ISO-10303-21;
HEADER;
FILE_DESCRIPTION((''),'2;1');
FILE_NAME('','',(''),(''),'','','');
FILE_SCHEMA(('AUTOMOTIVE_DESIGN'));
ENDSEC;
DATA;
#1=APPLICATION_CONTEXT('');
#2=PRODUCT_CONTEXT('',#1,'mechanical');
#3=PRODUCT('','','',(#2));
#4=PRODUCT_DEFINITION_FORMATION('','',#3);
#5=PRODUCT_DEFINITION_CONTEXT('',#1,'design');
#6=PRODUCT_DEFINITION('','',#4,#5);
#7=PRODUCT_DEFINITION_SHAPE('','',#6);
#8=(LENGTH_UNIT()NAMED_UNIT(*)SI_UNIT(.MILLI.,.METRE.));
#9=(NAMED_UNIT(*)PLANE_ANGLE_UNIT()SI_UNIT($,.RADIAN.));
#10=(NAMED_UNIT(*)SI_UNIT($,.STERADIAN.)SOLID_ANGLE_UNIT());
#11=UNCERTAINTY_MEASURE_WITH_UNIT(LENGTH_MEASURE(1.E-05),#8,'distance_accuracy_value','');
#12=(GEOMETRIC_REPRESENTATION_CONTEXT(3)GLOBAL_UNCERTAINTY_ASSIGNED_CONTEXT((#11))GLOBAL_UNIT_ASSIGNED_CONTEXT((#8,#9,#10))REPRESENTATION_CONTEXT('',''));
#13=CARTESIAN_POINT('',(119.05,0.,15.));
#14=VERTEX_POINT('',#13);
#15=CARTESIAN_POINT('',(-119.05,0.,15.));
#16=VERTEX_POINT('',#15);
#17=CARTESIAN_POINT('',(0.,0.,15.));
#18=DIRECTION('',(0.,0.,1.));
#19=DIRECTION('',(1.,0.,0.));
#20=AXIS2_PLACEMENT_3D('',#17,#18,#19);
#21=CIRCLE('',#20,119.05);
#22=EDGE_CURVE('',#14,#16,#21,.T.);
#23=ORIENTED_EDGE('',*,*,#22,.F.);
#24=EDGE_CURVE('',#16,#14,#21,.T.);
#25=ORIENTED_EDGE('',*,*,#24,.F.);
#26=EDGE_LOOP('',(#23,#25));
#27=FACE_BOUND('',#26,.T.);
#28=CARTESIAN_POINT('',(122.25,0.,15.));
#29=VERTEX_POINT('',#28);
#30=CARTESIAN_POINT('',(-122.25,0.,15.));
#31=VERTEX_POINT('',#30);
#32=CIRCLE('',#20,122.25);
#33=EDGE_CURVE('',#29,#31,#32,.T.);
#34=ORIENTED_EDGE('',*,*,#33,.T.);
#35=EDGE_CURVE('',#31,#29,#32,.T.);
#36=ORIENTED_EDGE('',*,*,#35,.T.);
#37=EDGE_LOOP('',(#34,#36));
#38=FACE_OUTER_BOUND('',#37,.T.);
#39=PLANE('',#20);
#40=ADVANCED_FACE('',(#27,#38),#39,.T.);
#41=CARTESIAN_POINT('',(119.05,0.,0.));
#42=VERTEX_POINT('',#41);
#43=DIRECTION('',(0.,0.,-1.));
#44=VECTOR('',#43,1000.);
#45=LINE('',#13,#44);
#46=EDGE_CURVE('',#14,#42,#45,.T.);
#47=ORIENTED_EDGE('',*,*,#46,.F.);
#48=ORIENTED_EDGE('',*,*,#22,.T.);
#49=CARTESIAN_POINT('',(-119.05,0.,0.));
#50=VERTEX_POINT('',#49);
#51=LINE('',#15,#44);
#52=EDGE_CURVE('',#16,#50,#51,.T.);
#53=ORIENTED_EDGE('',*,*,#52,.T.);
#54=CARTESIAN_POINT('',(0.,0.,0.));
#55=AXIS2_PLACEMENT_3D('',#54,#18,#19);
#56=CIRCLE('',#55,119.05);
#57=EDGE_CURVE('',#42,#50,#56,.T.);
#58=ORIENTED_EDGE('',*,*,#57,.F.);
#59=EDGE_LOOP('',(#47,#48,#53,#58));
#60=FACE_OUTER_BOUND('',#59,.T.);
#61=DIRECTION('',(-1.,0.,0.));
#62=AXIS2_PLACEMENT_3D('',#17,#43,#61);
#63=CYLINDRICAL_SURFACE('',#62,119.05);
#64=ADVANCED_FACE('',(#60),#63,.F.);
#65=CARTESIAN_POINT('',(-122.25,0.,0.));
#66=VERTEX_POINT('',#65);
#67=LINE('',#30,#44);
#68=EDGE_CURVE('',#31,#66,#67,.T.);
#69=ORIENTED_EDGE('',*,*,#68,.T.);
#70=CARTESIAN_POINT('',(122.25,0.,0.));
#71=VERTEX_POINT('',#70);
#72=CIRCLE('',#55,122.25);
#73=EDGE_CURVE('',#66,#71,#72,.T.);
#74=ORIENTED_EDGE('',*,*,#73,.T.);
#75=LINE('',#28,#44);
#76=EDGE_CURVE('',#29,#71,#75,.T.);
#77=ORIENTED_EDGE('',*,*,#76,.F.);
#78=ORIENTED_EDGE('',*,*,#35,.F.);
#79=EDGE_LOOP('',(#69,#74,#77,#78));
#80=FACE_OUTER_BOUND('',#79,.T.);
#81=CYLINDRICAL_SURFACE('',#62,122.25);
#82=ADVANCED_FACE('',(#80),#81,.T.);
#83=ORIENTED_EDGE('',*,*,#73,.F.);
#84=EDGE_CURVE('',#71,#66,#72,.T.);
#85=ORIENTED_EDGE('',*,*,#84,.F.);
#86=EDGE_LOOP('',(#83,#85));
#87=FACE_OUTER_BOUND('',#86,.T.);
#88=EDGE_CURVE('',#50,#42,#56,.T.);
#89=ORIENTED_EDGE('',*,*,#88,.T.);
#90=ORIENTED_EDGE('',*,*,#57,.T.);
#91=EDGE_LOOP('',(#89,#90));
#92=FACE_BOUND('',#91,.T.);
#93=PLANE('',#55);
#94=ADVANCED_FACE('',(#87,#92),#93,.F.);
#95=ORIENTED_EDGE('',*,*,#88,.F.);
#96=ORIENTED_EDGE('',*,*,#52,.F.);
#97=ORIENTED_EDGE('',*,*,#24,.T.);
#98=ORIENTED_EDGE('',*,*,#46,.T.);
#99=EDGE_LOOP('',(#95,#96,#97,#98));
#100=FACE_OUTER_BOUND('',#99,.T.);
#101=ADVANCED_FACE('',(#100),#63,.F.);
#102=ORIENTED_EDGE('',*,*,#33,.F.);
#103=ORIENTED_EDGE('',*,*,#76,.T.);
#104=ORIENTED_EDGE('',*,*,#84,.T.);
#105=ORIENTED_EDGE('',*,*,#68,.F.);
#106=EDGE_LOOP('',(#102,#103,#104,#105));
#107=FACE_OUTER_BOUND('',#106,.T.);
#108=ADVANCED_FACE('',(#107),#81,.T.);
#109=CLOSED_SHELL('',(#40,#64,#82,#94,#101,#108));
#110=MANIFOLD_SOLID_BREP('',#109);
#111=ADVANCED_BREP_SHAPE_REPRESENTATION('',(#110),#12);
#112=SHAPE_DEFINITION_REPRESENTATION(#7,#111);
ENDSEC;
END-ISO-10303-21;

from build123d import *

# Parameters (mm, degrees)
SKETCH_1_R      = 122.25
SKETCH_1_R_2    = 119.05
EXTRUDE_1_DEPTH = 15


with BuildPart() as part:
    # 草图1 → 凸台-拉伸1 (new body)
    with BuildSketch(Plane.XY):
        Circle(SKETCH_1_R)
        Circle(SKETCH_1_R_2, mode=Mode.SUBTRACT)
    extrude(amount=EXTRUDE_1_DEPTH)


solid = part.part
